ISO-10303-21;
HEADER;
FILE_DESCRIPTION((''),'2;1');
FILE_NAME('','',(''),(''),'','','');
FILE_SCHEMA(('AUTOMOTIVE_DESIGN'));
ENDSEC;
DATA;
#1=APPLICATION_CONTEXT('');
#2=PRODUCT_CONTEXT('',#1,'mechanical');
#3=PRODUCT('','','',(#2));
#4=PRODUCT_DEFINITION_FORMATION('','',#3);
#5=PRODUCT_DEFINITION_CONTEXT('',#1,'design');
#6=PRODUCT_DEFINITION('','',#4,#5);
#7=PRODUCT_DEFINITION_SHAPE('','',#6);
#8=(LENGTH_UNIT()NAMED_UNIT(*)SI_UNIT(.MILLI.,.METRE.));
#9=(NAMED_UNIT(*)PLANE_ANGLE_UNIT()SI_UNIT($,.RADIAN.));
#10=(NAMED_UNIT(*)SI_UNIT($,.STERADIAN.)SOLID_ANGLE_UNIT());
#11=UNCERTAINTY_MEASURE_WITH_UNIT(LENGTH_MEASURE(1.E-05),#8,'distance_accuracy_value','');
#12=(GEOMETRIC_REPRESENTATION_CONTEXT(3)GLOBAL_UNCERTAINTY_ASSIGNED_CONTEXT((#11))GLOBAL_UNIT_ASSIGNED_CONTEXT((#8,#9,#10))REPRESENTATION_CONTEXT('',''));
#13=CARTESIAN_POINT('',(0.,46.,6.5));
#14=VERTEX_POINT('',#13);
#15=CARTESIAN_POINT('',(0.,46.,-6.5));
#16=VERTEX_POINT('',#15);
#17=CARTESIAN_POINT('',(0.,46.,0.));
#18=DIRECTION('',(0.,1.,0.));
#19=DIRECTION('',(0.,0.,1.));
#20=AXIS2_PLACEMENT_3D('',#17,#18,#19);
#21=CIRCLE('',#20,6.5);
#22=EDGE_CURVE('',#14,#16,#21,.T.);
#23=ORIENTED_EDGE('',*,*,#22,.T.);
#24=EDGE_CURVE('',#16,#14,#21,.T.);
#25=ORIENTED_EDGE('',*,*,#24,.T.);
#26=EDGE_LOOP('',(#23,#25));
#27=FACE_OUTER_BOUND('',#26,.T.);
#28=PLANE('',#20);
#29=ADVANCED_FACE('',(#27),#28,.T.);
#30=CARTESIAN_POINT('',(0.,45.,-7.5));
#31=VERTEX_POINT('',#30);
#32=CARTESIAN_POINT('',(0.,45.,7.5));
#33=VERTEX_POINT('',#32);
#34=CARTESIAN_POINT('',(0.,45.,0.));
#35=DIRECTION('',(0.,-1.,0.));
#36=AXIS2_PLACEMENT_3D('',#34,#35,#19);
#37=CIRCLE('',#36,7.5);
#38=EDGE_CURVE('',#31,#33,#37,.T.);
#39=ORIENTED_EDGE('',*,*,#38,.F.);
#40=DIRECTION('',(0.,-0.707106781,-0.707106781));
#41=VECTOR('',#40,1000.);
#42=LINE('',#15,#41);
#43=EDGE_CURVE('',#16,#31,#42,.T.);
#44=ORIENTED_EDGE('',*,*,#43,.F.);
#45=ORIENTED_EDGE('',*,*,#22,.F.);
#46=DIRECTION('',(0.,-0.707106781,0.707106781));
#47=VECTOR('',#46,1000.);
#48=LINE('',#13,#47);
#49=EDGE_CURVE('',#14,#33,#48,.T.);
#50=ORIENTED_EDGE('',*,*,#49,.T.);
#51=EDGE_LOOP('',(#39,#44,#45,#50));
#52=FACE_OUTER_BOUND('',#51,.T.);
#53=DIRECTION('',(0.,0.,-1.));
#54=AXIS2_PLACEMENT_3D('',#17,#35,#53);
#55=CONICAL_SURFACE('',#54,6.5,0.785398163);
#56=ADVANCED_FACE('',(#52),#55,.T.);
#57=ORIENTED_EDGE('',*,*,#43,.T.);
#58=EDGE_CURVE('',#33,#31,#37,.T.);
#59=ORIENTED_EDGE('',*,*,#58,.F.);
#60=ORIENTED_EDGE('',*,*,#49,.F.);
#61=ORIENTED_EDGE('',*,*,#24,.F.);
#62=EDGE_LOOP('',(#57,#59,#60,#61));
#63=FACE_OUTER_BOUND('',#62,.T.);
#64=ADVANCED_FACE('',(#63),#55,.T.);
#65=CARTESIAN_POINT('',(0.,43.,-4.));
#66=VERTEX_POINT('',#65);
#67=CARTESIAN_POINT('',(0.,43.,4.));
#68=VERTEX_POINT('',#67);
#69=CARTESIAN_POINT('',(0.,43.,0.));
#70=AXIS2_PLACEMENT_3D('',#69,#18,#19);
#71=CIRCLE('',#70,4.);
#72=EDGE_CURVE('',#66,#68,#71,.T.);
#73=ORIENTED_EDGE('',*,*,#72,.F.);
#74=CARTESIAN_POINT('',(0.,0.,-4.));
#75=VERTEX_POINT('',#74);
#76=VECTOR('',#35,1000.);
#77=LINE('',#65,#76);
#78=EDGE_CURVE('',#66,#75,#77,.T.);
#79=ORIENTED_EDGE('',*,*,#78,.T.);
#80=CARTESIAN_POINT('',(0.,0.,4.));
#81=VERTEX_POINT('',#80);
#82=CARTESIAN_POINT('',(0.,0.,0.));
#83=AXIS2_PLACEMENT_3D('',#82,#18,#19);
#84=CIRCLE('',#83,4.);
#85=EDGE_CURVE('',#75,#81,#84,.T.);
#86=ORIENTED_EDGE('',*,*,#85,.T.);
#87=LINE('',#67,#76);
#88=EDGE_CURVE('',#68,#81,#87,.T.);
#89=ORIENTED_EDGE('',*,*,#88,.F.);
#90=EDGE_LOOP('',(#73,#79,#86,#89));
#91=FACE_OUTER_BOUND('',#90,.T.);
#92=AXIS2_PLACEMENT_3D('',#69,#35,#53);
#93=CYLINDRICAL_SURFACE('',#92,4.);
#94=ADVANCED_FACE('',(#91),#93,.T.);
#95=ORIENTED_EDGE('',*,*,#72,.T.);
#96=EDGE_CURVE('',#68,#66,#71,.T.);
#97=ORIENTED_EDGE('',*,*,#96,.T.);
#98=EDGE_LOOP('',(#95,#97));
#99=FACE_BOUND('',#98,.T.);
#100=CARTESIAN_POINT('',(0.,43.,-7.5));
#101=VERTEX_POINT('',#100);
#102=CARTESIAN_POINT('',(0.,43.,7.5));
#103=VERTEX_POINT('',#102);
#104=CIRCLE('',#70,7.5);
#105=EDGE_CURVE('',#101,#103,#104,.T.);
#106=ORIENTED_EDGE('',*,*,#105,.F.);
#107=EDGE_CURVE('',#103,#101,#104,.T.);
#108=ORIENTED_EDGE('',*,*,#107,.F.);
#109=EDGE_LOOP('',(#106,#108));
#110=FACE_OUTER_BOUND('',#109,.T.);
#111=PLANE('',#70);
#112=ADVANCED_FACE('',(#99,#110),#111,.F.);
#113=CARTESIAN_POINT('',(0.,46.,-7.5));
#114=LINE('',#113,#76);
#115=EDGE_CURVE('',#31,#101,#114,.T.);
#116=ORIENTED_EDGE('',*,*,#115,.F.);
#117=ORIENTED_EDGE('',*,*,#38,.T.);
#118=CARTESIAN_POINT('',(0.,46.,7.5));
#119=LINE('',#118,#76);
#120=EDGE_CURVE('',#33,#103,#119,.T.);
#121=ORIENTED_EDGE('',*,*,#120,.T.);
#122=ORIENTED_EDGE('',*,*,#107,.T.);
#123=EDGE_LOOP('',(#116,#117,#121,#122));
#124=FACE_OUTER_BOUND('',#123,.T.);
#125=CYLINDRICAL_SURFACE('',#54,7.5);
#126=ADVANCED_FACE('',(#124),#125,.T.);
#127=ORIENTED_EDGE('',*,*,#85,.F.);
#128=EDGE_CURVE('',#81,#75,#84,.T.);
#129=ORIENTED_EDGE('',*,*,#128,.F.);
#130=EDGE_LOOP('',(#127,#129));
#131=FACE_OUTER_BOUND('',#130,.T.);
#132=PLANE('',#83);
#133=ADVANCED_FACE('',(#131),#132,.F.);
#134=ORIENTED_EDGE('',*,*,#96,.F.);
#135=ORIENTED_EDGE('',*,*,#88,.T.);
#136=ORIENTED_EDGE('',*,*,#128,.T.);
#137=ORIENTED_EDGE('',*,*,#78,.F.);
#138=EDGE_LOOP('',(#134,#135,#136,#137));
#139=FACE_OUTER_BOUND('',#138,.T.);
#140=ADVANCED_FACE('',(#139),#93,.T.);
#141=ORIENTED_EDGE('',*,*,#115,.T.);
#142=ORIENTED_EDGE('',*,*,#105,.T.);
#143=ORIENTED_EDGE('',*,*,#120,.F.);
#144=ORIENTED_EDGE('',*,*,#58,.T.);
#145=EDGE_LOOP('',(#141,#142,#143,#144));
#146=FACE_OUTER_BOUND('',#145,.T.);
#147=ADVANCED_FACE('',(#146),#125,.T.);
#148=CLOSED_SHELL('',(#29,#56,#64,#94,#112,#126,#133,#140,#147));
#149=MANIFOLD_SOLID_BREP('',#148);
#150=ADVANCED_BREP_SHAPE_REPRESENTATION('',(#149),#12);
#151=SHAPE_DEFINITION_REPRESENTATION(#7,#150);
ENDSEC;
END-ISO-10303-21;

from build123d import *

# Parameters (mm, degrees)
SHANK_PROFILE_8_R           = 4
SHANK_8X43_DEPTH            = 43
HEAD_PROFILE_15_R           = 7.5
HEAD_15X3_DEPTH             = 3
HEAD_EDGE_CHAMFER_1X45_SIZE = 1


with BuildPart() as part:
    # Shank Profile Ø8 → Shank Ø8x43 (new body)
    with BuildSketch(Plane(origin=(0, 0, 0), x_dir=(1, 0, 0), z_dir=(0, 1, 0))):
        with Locations(Location((0, 0, 0), (0, 0, 270))):
            Circle(SHANK_PROFILE_8_R)
    extrude(amount=SHANK_8X43_DEPTH)

    # Head Profile Ø15 → Head Ø15x3 (add)
    with BuildSketch(Plane(origin=(0, 43, 0), x_dir=(1, 0, 0), z_dir=(0, 1, 0))):
        with Locations(Location((0, 0, 0), (0, 0, 270))):
            Circle(HEAD_PROFILE_15_R)
    extrude(amount=HEAD_15X3_DEPTH)

    # Head Edge Chamfer 1x45°
    head_edge_chamfer_1x45_edges = [part.edges().sort_by_distance(p)[0] for p in [
        (0, 46, -7.5),
    ]]
    chamfer(head_edge_chamfer_1x45_edges, length=HEAD_EDGE_CHAMFER_1X45_SIZE)


solid = part.part
